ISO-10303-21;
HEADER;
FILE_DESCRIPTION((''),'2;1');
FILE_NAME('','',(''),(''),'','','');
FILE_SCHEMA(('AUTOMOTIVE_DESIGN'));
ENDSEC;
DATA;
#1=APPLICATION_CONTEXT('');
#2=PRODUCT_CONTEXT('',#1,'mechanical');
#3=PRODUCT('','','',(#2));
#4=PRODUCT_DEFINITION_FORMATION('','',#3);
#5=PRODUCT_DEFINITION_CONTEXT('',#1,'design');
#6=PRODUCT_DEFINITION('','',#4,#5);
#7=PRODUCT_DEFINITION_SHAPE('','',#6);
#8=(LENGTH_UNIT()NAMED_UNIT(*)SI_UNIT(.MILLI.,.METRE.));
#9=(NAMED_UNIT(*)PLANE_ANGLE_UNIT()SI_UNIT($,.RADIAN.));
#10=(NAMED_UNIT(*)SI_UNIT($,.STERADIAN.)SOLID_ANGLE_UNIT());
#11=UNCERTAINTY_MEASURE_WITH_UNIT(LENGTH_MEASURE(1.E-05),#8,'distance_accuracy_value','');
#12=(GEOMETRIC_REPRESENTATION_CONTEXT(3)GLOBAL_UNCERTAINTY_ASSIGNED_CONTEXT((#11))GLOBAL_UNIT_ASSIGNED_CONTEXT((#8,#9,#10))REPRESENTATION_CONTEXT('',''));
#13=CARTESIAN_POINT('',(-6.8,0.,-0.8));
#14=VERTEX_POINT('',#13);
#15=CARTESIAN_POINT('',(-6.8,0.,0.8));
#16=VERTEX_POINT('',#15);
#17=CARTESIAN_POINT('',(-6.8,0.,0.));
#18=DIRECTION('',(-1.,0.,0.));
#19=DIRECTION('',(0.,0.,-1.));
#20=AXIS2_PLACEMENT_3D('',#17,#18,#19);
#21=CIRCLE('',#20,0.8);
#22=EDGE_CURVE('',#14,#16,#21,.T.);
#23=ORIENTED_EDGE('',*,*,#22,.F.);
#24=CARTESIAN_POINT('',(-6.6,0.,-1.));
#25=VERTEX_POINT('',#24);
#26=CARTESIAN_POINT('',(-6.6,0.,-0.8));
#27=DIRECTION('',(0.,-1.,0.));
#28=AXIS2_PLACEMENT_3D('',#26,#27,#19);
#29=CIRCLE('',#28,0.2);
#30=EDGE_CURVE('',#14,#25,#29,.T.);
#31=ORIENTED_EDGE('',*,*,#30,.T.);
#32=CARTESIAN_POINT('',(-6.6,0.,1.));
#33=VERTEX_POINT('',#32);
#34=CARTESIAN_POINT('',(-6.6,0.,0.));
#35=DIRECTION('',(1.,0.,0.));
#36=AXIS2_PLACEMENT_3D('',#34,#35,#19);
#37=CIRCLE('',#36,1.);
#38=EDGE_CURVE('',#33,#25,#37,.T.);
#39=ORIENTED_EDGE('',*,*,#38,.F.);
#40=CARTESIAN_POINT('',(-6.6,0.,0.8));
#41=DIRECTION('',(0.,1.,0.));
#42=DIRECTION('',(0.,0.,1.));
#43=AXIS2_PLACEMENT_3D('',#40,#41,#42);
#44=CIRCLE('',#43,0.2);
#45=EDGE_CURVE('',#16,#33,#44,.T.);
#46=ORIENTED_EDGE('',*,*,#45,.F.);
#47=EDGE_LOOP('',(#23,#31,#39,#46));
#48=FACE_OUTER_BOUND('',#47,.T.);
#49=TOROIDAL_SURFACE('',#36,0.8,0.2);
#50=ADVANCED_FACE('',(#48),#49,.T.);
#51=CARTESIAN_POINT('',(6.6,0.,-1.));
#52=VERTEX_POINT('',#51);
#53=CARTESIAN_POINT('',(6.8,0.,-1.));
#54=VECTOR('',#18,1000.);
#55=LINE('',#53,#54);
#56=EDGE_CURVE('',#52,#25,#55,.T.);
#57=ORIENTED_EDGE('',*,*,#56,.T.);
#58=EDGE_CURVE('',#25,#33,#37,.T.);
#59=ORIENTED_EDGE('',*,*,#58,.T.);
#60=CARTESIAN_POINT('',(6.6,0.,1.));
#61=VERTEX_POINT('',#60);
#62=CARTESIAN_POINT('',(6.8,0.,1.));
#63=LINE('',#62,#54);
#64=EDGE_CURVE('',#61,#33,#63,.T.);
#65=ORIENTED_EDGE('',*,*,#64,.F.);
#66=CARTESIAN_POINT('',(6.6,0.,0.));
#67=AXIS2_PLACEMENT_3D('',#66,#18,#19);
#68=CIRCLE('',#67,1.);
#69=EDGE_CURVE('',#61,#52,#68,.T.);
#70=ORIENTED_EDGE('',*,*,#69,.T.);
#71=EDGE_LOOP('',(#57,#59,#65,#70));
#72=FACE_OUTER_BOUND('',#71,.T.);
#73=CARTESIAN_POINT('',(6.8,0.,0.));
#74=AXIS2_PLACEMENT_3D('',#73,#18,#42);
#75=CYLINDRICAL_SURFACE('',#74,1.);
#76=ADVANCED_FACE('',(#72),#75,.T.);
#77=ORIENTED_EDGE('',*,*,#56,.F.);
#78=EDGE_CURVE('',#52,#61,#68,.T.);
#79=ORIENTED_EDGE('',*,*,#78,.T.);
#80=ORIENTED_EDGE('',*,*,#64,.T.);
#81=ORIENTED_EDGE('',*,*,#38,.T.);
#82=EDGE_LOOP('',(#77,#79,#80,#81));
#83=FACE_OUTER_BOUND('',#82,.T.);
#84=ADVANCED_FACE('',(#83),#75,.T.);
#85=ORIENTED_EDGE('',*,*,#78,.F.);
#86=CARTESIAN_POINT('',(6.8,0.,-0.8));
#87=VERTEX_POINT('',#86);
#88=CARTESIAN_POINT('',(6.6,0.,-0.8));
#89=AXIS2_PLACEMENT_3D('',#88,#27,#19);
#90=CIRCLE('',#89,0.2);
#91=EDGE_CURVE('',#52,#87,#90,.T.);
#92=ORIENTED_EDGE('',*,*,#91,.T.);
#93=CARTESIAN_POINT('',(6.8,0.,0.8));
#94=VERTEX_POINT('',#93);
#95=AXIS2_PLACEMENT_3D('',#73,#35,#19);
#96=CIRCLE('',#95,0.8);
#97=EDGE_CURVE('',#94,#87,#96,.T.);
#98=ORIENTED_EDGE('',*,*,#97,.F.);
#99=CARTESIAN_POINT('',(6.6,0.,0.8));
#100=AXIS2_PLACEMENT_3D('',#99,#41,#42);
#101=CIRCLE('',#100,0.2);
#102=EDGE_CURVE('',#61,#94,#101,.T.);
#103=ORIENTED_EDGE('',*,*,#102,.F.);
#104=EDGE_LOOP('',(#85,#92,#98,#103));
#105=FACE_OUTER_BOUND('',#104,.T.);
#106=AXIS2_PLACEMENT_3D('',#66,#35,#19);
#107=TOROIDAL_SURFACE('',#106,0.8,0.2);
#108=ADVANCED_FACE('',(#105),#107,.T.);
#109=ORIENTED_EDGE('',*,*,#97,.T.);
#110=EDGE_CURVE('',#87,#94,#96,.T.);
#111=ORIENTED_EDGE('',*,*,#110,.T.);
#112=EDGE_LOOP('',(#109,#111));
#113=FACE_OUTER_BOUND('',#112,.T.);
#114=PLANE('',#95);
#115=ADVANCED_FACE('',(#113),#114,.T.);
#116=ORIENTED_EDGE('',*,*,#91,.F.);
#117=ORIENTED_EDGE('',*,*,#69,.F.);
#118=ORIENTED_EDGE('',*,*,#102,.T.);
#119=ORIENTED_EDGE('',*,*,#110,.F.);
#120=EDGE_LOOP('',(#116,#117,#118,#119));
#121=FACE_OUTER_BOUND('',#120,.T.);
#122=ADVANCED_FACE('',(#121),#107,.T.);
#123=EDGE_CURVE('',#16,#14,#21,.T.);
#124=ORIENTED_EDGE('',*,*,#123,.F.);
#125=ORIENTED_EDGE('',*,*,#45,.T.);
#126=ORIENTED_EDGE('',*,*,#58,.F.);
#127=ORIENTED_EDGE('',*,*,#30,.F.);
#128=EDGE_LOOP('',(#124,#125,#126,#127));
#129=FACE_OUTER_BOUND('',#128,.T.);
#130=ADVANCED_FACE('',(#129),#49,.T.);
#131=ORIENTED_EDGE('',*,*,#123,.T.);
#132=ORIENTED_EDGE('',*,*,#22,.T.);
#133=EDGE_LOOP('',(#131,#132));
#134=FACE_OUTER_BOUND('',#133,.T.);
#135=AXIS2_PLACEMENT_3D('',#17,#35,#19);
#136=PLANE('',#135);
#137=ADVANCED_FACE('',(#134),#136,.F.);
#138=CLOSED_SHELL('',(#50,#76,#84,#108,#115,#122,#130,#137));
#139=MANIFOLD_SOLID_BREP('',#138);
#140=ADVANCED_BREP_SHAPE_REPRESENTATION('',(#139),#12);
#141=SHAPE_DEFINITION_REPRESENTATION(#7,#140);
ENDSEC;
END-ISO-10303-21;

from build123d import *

# Parameters (mm, degrees)
SKETCH_1_R      = 1
EXTRUDE_1_DEPTH = 6.8
FILLET_1_R      = 0.2


with BuildPart() as part:
    # 草图1 → 凸台-拉伸1 (new, symmetric)
    with BuildSketch(Plane(origin=(0, 0, 0), x_dir=(0, 0, -1), z_dir=(1, 0, 0))):
        Circle(SKETCH_1_R)
    extrude(amount=EXTRUDE_1_DEPTH, both=True)

    # 圆角1
    fillet_1_edges = [part.edges().sort_by_distance(p)[0] for p in [
        (-6.8, 0, 1),
        (6.8, 0, 1),
    ]]
    fillet(fillet_1_edges, radius=FILLET_1_R)


solid = part.part
